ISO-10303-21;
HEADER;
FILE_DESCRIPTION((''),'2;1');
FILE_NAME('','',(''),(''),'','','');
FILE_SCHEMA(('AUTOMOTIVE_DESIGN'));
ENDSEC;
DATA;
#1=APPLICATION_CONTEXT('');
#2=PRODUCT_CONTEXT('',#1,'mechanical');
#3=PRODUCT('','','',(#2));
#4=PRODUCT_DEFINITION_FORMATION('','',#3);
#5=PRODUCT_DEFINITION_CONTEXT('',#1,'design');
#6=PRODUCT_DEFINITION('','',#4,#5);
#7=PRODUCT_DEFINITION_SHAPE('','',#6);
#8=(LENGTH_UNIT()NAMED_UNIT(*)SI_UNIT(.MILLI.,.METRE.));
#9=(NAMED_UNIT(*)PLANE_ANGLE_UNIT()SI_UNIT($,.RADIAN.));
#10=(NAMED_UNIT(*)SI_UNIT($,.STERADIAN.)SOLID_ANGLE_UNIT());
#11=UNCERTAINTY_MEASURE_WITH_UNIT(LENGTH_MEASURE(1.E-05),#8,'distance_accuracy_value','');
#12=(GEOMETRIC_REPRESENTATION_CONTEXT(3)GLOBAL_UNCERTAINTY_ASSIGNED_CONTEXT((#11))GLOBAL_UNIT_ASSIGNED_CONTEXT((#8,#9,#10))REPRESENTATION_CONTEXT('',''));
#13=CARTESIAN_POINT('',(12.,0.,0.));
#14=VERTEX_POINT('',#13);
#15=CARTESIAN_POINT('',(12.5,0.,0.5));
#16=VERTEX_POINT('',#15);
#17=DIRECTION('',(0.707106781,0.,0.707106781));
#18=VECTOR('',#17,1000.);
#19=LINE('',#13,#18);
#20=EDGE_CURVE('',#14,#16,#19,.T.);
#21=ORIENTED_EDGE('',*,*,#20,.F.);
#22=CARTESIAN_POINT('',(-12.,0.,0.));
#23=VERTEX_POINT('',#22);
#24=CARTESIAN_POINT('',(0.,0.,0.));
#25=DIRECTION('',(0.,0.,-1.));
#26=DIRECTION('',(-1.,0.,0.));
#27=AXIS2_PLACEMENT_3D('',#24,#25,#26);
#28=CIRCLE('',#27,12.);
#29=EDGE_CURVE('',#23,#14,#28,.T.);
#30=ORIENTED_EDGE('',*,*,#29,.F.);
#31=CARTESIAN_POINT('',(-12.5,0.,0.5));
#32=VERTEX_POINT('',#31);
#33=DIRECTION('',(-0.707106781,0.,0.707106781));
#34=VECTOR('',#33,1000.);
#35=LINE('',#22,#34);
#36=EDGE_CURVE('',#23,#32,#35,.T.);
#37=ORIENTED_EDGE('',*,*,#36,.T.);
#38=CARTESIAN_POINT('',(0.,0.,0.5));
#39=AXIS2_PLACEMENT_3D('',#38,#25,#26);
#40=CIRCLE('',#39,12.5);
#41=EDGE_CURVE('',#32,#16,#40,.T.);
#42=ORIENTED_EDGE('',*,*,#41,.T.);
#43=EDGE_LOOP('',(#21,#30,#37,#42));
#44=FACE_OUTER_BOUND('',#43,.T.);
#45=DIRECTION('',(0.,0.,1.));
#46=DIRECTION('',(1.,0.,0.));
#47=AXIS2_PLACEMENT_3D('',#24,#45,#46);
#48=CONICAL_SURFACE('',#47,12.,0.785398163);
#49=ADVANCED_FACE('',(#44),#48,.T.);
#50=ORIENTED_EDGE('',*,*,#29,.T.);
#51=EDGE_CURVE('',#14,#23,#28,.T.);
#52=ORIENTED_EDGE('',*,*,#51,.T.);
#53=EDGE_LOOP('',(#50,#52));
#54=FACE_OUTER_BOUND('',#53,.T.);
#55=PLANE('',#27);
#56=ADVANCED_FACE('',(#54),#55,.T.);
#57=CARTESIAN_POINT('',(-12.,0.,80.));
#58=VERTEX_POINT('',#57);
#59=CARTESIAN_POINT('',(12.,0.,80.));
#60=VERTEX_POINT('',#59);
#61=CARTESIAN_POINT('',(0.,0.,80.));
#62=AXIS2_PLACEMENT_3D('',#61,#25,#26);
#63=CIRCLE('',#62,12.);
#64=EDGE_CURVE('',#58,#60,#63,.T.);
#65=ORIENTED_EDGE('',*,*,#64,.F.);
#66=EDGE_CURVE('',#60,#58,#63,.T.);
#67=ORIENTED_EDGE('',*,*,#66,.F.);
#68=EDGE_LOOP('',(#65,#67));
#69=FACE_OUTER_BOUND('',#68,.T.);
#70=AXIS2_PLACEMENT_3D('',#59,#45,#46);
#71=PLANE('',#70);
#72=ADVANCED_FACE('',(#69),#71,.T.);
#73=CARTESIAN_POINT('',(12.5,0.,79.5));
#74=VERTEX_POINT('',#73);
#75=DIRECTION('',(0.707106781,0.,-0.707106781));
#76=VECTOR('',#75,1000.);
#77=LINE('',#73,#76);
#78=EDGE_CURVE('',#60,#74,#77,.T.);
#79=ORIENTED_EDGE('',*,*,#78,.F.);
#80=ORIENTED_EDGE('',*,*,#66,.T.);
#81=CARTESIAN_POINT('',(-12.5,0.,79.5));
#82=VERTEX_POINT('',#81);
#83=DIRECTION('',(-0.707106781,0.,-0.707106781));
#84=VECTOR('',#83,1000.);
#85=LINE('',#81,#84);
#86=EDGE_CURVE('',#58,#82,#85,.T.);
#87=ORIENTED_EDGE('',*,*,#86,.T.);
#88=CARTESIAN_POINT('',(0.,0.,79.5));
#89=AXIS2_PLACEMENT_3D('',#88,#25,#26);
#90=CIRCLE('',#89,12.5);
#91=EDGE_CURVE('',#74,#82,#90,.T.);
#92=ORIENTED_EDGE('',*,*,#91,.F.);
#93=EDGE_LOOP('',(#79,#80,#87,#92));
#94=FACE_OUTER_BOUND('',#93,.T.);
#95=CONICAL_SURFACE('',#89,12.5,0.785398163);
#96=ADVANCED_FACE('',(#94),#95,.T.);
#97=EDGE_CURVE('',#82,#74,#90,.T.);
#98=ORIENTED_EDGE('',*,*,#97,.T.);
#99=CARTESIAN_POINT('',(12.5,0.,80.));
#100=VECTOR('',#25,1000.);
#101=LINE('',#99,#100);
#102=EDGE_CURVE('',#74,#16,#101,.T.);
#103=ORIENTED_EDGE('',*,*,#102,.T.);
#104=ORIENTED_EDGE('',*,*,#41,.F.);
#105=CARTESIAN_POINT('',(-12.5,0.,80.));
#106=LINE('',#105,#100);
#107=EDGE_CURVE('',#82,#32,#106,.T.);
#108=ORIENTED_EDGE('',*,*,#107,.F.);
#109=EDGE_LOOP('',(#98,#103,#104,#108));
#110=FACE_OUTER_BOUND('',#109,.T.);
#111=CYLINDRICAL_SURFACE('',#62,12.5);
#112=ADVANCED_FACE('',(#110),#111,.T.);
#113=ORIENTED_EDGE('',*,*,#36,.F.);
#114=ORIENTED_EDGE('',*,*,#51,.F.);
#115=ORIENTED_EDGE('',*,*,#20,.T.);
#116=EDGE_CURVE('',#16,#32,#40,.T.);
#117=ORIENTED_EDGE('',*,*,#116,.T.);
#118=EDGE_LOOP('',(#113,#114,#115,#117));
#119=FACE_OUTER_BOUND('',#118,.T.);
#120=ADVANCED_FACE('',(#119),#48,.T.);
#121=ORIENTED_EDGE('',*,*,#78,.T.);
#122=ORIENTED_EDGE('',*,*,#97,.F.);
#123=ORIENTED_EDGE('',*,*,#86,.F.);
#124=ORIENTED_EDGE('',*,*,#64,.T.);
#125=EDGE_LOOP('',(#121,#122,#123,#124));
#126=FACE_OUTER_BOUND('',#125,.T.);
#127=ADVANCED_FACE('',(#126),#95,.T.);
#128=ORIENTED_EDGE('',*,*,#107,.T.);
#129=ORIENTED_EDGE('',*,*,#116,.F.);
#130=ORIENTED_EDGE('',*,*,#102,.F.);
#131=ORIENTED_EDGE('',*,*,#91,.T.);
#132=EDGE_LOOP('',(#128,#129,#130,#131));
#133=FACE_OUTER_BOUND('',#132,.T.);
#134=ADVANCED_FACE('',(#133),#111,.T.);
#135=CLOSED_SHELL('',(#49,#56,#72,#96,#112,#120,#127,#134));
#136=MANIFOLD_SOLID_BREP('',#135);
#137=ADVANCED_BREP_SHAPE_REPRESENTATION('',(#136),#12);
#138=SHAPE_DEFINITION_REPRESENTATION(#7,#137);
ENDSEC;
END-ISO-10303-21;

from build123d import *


with BuildPart() as part:
    # Sketch1 → Revolve1 (revolve)
    with BuildSketch(Plane.XZ, mode=Mode.PRIVATE) as revolve1_sk:
        Polygon((12, 80), (0, 80), (0, 0), (12, 0), (12.5, 0.5), (12.5, 79.5), align=None)
    revolve(revolve1_sk.sketch.rotate(Axis((0, 0, 80), (0, 0, -1)), 180), axis=Axis((0, 0, 80), (0, 0, -1)))


solid = part.part
